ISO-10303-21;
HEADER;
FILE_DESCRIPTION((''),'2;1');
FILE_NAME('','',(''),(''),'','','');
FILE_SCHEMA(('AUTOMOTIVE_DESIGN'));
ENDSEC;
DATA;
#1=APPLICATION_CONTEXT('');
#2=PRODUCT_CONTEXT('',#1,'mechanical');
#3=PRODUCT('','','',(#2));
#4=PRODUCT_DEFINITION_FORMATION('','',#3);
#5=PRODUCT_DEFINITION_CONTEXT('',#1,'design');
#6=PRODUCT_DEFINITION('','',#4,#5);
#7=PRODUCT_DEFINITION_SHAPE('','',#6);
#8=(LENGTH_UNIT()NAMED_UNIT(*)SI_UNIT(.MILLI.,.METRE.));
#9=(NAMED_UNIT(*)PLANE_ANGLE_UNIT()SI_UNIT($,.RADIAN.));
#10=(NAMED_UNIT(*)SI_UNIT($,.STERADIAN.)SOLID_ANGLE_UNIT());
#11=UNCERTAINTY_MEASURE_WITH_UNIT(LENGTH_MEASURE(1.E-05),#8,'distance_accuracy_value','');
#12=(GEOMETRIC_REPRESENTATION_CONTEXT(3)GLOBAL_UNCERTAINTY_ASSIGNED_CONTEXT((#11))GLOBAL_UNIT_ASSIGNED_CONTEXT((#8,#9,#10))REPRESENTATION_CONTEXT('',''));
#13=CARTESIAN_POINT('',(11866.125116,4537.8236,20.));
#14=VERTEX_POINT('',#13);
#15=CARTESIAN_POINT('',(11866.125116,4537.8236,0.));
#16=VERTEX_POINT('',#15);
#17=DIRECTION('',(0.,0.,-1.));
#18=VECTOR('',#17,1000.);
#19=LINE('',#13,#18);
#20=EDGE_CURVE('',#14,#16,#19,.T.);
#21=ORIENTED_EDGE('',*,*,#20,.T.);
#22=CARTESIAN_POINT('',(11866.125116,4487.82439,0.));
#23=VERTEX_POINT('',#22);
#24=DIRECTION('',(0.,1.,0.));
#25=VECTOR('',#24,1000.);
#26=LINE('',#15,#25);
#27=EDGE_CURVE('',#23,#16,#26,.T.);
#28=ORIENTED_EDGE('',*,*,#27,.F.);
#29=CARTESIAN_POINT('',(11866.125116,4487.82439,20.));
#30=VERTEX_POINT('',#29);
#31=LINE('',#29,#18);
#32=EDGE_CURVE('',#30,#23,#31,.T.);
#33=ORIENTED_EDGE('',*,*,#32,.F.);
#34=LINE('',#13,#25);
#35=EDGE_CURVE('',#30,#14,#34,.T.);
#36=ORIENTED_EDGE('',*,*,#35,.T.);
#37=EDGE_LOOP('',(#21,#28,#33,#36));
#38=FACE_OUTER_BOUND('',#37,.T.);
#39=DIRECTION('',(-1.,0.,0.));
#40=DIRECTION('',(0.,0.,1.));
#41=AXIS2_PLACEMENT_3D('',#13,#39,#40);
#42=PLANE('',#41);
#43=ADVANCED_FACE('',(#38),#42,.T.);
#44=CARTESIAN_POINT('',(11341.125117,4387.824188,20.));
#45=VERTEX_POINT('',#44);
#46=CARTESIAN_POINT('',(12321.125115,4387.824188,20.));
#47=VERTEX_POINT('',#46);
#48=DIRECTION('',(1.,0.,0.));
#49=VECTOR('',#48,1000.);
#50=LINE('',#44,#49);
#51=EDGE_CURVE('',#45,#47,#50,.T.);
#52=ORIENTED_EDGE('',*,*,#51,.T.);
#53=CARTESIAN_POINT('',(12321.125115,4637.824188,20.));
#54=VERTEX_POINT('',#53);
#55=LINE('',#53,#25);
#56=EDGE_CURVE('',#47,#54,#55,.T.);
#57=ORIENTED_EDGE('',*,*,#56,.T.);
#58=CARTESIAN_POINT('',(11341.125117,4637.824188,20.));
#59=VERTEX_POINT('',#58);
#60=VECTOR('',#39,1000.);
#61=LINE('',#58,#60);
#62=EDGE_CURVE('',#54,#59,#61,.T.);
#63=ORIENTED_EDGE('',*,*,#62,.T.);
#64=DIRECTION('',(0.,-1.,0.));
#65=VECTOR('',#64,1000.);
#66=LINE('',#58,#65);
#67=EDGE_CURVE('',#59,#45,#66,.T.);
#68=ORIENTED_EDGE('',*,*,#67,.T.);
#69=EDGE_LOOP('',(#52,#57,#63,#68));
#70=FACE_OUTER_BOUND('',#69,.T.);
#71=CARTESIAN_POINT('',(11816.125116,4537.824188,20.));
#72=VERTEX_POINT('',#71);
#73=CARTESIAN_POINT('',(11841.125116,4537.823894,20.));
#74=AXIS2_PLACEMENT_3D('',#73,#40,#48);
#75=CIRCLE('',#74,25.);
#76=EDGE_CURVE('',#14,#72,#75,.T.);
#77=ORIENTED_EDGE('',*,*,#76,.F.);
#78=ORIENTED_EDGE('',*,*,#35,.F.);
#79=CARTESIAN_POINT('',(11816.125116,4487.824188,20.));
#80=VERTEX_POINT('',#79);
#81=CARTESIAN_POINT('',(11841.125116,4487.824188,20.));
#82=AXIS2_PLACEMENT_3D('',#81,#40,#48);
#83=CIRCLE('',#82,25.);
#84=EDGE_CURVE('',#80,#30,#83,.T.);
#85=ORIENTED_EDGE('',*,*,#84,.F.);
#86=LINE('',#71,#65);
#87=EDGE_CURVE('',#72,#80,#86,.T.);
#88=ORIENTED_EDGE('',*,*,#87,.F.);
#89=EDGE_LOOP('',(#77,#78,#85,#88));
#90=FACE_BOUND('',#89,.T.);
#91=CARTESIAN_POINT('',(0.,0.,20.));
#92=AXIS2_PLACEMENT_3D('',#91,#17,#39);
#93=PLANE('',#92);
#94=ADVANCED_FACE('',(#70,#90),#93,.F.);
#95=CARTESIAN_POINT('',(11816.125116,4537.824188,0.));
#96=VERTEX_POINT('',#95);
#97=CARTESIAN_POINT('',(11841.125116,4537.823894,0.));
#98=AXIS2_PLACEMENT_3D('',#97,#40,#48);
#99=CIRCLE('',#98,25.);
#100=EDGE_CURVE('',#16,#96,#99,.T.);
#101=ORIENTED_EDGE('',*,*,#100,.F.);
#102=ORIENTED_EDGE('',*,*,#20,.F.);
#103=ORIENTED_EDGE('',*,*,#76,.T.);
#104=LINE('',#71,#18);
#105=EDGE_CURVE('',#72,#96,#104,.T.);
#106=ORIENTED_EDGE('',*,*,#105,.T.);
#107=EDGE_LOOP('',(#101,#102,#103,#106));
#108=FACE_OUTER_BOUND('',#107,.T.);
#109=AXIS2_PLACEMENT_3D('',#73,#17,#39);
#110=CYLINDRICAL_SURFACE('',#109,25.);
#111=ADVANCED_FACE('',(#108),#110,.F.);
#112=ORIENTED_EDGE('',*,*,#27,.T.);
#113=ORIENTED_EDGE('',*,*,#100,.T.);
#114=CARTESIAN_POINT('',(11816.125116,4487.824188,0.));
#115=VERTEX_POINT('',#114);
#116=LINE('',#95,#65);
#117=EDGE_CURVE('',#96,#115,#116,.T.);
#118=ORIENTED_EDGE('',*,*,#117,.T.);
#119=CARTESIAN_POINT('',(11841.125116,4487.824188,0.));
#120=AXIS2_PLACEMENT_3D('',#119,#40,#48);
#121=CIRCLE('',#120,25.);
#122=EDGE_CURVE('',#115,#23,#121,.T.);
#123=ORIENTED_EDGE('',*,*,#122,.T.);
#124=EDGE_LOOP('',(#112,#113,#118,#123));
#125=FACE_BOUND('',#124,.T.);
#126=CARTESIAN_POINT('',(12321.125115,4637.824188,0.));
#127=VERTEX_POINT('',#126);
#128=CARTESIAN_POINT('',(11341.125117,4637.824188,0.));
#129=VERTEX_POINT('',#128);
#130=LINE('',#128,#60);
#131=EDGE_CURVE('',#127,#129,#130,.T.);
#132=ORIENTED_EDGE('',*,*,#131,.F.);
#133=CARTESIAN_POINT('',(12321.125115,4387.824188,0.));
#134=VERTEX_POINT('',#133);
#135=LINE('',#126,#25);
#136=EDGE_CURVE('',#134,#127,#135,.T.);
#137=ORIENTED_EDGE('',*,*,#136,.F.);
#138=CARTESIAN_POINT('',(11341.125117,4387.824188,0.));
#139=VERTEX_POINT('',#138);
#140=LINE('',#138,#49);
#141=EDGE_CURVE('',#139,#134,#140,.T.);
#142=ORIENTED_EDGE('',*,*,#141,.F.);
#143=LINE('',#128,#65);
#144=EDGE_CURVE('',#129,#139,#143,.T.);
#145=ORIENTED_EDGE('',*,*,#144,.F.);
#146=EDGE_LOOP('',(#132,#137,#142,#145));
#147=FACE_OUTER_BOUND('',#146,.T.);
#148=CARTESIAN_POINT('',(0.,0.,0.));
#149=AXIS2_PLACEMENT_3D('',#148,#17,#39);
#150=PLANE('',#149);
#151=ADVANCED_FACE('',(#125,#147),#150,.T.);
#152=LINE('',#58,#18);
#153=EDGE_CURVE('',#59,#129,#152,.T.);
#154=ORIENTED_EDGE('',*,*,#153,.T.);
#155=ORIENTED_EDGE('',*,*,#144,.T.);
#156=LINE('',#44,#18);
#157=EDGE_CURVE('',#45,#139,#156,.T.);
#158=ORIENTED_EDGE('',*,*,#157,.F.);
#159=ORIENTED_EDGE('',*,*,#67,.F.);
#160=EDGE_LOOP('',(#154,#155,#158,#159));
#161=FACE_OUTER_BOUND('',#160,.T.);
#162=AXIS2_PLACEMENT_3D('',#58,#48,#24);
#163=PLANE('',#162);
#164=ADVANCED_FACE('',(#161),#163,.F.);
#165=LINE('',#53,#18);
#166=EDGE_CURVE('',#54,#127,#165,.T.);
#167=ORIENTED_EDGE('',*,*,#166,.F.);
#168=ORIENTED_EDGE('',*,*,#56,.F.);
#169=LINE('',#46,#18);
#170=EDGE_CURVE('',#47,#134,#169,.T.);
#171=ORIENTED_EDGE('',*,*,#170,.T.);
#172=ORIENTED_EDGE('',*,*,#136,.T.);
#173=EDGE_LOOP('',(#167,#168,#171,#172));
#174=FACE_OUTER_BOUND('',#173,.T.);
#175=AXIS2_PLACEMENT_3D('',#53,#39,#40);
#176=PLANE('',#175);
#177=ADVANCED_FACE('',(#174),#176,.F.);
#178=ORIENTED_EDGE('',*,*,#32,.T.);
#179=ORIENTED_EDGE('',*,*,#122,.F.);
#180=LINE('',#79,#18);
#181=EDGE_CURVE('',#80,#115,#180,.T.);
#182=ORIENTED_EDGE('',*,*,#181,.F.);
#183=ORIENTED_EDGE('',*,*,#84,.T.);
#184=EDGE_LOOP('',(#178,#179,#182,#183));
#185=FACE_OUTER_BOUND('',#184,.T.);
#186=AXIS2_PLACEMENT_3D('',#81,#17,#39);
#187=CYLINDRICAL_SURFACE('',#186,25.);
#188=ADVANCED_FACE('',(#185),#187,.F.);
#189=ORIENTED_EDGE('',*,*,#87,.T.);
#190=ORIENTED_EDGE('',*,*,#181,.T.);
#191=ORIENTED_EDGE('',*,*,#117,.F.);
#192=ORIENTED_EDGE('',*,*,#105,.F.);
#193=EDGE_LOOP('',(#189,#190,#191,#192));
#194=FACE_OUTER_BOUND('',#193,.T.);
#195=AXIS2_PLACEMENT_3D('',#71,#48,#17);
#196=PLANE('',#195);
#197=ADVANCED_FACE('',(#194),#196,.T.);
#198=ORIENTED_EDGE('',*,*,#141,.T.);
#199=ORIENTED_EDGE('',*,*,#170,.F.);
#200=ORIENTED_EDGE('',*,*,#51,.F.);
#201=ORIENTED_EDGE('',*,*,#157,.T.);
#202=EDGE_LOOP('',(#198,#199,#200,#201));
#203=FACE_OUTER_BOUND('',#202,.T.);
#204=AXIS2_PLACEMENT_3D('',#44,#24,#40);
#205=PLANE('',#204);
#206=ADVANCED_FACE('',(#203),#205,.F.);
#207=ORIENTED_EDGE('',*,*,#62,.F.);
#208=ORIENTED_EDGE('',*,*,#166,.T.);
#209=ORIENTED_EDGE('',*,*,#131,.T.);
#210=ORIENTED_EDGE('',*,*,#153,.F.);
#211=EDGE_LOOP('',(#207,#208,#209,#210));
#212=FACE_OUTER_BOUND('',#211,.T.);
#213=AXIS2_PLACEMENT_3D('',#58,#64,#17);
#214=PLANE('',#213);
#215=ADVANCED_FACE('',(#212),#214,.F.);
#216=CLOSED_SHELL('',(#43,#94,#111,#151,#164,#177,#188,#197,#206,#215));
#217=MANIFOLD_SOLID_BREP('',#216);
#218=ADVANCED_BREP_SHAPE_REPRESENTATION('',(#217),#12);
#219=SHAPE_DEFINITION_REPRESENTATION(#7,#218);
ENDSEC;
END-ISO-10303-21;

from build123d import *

# Parameters (mm, degrees)
BOSS_EXTRUDE1_DEPTH = 20


with BuildPart() as part:
    # Sketch1 → Boss-Extrude1 (new body)
    with BuildSketch(Plane.XY):
        Polygon((11341.12511676, 4637.824188368), (11341.125116846, 4387.824188368), (12321.125115149, 4387.824188368), (12321.125115149, 4637.824188368), align=None)
        with BuildLine():
            Line((11816.125116094, 4537.824187896), (11816.125116094, 4487.824187992))
            ThreePointArc((11816.125116094, 4487.824187992), (11841.125216971, 4462.824188038), (11866.125116001, 4487.824389839))
            Line((11866.125116001, 4487.824389839), (11866.125116001, 4537.823600328))
            ThreePointArc((11866.125116001, 4537.823600328), (11841.125409832, 4562.823894066), (11816.125116094, 4537.824187896))
        make_face(mode=Mode.SUBTRACT)
    extrude(amount=BOSS_EXTRUDE1_DEPTH)


solid = part.part
